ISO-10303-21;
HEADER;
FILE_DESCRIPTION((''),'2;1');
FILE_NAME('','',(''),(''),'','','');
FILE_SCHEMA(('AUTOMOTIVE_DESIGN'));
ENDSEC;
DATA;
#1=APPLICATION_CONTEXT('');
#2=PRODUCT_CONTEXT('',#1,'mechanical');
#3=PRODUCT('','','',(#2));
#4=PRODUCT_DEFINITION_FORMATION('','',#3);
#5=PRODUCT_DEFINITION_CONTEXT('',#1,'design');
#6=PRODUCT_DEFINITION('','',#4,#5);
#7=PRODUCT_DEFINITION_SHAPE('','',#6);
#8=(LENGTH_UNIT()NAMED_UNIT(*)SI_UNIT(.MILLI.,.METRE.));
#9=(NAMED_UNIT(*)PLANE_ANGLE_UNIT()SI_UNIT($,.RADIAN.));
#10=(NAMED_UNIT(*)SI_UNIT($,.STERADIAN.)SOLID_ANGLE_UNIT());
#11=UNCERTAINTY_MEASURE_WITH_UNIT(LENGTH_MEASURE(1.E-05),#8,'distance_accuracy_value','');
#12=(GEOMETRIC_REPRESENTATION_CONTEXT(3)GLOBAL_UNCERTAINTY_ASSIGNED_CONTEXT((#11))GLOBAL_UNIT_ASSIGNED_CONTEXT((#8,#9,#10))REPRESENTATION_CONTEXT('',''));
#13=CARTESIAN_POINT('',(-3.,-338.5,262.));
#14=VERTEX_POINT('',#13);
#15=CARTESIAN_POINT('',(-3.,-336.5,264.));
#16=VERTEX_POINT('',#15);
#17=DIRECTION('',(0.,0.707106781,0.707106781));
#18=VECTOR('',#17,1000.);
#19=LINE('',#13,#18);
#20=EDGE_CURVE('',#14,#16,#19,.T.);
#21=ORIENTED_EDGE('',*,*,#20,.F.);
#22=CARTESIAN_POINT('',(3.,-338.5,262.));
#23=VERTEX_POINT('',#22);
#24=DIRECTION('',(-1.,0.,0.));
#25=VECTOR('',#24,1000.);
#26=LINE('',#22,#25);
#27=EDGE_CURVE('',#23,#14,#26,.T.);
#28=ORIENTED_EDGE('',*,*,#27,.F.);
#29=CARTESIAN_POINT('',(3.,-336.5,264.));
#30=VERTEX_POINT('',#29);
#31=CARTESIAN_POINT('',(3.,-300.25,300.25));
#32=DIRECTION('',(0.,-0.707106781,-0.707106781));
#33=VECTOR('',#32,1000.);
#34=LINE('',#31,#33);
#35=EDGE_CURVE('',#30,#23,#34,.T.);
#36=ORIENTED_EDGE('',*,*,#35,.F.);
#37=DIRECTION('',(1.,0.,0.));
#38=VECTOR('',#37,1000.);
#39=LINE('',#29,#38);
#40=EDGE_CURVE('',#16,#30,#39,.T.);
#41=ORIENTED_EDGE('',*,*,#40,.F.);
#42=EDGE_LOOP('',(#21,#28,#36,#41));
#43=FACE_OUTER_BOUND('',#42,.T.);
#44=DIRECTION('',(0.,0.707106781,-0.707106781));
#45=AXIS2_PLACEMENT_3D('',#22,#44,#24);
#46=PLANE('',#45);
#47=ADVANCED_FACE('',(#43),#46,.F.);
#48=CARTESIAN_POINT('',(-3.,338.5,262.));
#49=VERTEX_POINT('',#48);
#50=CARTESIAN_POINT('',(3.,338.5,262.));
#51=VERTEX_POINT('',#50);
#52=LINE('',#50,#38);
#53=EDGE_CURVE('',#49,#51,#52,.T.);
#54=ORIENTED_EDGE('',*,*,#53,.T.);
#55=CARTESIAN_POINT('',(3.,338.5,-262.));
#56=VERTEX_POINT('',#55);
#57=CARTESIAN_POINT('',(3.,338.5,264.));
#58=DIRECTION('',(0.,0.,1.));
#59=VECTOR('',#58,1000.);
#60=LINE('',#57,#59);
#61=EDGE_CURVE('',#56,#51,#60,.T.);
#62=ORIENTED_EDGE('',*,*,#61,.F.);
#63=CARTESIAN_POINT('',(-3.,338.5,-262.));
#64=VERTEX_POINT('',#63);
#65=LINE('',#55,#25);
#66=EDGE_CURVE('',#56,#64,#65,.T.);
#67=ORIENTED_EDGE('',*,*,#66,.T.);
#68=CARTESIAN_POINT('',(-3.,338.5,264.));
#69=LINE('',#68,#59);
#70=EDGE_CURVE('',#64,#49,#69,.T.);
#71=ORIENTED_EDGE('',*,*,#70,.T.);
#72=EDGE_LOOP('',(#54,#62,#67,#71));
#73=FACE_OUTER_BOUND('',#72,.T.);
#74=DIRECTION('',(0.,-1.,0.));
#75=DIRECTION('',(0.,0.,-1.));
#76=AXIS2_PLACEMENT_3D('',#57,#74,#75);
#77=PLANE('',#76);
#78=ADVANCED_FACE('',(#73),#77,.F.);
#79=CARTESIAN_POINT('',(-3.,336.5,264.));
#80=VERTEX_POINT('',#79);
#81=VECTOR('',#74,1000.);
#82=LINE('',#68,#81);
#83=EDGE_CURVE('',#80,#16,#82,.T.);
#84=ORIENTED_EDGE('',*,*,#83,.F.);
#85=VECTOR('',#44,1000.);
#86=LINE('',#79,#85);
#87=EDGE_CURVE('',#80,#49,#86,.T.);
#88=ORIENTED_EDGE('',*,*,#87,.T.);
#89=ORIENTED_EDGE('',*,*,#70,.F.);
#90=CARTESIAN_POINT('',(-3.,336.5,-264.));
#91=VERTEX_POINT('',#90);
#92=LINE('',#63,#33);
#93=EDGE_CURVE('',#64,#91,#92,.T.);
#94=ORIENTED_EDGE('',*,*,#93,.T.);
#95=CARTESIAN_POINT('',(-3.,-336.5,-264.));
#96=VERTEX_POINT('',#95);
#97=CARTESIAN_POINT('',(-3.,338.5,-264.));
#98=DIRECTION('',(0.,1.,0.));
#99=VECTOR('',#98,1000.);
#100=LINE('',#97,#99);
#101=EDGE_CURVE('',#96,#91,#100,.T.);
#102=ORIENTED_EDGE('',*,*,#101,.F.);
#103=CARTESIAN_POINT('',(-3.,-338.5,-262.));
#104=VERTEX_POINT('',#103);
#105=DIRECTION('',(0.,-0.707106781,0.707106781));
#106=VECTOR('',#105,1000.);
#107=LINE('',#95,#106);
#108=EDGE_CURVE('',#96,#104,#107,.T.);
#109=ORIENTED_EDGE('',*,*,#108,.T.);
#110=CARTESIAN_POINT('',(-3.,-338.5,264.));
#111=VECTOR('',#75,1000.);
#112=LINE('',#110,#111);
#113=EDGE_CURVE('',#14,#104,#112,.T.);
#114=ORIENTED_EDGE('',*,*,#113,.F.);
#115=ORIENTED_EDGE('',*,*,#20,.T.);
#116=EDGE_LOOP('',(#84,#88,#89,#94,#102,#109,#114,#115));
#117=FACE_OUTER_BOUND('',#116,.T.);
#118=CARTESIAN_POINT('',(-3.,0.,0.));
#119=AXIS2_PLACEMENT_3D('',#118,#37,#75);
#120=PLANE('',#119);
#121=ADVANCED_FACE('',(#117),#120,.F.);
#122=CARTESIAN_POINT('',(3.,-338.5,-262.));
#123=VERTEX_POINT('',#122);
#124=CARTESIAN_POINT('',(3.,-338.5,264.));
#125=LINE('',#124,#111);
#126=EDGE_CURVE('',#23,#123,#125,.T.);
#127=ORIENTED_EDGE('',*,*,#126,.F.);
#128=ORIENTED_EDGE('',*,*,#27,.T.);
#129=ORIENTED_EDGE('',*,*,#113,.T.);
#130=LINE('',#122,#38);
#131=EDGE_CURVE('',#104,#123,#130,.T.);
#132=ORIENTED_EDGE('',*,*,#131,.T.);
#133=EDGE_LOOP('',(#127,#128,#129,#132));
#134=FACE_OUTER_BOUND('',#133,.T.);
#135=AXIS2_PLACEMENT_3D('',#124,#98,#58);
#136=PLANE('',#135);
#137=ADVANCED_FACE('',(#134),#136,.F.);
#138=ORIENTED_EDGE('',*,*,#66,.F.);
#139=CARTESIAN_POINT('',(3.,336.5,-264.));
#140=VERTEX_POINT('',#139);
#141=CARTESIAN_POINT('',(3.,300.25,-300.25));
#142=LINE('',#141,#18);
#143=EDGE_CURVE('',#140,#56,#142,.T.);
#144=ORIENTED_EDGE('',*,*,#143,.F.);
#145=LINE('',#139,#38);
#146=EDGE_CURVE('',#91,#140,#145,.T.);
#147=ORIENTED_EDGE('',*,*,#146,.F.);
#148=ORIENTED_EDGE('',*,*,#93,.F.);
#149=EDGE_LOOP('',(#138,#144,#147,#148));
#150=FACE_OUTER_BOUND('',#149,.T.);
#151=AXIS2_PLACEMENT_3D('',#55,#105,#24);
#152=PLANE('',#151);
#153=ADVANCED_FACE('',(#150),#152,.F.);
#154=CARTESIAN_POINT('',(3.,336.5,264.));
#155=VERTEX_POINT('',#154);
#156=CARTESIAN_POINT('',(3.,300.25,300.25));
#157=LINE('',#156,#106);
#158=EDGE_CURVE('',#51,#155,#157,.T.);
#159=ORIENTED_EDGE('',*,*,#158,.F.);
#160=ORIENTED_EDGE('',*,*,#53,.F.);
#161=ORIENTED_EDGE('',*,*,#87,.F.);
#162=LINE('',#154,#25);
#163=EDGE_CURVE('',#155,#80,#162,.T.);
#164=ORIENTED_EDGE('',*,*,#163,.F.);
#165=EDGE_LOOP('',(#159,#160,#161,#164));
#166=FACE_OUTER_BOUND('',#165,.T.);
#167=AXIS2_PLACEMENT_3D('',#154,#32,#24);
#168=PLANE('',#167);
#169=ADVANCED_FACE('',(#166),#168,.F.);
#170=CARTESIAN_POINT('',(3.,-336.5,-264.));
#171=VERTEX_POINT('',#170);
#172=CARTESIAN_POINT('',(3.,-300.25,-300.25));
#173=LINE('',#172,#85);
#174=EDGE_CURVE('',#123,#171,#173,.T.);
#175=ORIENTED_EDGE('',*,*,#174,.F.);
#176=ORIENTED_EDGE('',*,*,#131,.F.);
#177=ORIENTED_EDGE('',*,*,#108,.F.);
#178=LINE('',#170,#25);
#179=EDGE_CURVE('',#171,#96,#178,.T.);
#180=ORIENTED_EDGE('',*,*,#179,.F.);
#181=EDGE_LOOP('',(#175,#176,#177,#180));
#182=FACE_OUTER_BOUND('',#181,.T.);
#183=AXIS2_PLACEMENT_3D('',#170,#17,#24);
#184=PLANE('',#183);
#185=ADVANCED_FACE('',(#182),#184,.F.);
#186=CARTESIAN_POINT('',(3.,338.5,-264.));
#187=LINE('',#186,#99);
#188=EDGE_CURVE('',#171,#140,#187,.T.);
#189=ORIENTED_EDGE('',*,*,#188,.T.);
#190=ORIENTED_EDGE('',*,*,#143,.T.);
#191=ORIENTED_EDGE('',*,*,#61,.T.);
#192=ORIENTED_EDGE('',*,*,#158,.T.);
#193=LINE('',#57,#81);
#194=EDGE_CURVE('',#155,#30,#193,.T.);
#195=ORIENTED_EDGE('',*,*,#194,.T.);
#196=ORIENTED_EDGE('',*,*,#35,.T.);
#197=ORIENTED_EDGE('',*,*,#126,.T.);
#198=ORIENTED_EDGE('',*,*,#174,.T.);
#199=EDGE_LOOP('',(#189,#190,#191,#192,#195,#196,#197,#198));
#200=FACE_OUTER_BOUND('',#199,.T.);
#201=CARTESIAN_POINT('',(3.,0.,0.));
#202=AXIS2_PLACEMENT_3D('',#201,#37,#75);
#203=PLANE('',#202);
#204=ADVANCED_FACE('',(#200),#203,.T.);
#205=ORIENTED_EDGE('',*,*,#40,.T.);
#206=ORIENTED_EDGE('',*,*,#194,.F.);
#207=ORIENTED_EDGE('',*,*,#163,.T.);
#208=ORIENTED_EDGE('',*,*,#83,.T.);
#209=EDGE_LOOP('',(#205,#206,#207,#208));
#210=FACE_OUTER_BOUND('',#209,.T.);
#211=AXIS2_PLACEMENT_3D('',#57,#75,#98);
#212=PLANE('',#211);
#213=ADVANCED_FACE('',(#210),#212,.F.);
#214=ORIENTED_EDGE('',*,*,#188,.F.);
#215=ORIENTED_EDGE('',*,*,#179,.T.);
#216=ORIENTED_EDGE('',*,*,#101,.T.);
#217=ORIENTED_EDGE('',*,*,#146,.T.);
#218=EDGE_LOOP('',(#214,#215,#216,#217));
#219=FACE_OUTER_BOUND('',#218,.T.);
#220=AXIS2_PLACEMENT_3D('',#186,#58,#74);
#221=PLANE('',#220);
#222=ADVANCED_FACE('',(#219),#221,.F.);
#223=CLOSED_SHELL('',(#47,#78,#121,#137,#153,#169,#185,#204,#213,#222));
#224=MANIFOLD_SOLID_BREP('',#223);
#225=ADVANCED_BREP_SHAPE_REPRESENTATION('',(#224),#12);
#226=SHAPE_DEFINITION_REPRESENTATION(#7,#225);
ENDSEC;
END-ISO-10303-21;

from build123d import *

# Parameters (mm, degrees)
SKETCH_1_W      = 528
SKETCH_1_H      = 677
EXTRUDE_1_DEPTH = 3
CHAMFER_1_SIZE  = 2


with BuildPart() as part:
    # 草图1 → 凸台-拉伸1 (new, symmetric)
    with BuildSketch(Plane(origin=(0, 0, 0), x_dir=(0, 0, -1), z_dir=(1, 0, 0))):
        Rectangle(SKETCH_1_W, SKETCH_1_H)
    extrude(amount=EXTRUDE_1_DEPTH, both=True)

    # 倒角1
    chamfer_1_edges = [part.edges().sort_by_distance(p)[0] for p in [
        (0, -338.5, -264),
        (0, -338.5, 264),
        (0, 338.5, 264),
        (0, 338.5, -264),
    ]]
    chamfer(chamfer_1_edges, length=CHAMFER_1_SIZE)


solid = part.part
